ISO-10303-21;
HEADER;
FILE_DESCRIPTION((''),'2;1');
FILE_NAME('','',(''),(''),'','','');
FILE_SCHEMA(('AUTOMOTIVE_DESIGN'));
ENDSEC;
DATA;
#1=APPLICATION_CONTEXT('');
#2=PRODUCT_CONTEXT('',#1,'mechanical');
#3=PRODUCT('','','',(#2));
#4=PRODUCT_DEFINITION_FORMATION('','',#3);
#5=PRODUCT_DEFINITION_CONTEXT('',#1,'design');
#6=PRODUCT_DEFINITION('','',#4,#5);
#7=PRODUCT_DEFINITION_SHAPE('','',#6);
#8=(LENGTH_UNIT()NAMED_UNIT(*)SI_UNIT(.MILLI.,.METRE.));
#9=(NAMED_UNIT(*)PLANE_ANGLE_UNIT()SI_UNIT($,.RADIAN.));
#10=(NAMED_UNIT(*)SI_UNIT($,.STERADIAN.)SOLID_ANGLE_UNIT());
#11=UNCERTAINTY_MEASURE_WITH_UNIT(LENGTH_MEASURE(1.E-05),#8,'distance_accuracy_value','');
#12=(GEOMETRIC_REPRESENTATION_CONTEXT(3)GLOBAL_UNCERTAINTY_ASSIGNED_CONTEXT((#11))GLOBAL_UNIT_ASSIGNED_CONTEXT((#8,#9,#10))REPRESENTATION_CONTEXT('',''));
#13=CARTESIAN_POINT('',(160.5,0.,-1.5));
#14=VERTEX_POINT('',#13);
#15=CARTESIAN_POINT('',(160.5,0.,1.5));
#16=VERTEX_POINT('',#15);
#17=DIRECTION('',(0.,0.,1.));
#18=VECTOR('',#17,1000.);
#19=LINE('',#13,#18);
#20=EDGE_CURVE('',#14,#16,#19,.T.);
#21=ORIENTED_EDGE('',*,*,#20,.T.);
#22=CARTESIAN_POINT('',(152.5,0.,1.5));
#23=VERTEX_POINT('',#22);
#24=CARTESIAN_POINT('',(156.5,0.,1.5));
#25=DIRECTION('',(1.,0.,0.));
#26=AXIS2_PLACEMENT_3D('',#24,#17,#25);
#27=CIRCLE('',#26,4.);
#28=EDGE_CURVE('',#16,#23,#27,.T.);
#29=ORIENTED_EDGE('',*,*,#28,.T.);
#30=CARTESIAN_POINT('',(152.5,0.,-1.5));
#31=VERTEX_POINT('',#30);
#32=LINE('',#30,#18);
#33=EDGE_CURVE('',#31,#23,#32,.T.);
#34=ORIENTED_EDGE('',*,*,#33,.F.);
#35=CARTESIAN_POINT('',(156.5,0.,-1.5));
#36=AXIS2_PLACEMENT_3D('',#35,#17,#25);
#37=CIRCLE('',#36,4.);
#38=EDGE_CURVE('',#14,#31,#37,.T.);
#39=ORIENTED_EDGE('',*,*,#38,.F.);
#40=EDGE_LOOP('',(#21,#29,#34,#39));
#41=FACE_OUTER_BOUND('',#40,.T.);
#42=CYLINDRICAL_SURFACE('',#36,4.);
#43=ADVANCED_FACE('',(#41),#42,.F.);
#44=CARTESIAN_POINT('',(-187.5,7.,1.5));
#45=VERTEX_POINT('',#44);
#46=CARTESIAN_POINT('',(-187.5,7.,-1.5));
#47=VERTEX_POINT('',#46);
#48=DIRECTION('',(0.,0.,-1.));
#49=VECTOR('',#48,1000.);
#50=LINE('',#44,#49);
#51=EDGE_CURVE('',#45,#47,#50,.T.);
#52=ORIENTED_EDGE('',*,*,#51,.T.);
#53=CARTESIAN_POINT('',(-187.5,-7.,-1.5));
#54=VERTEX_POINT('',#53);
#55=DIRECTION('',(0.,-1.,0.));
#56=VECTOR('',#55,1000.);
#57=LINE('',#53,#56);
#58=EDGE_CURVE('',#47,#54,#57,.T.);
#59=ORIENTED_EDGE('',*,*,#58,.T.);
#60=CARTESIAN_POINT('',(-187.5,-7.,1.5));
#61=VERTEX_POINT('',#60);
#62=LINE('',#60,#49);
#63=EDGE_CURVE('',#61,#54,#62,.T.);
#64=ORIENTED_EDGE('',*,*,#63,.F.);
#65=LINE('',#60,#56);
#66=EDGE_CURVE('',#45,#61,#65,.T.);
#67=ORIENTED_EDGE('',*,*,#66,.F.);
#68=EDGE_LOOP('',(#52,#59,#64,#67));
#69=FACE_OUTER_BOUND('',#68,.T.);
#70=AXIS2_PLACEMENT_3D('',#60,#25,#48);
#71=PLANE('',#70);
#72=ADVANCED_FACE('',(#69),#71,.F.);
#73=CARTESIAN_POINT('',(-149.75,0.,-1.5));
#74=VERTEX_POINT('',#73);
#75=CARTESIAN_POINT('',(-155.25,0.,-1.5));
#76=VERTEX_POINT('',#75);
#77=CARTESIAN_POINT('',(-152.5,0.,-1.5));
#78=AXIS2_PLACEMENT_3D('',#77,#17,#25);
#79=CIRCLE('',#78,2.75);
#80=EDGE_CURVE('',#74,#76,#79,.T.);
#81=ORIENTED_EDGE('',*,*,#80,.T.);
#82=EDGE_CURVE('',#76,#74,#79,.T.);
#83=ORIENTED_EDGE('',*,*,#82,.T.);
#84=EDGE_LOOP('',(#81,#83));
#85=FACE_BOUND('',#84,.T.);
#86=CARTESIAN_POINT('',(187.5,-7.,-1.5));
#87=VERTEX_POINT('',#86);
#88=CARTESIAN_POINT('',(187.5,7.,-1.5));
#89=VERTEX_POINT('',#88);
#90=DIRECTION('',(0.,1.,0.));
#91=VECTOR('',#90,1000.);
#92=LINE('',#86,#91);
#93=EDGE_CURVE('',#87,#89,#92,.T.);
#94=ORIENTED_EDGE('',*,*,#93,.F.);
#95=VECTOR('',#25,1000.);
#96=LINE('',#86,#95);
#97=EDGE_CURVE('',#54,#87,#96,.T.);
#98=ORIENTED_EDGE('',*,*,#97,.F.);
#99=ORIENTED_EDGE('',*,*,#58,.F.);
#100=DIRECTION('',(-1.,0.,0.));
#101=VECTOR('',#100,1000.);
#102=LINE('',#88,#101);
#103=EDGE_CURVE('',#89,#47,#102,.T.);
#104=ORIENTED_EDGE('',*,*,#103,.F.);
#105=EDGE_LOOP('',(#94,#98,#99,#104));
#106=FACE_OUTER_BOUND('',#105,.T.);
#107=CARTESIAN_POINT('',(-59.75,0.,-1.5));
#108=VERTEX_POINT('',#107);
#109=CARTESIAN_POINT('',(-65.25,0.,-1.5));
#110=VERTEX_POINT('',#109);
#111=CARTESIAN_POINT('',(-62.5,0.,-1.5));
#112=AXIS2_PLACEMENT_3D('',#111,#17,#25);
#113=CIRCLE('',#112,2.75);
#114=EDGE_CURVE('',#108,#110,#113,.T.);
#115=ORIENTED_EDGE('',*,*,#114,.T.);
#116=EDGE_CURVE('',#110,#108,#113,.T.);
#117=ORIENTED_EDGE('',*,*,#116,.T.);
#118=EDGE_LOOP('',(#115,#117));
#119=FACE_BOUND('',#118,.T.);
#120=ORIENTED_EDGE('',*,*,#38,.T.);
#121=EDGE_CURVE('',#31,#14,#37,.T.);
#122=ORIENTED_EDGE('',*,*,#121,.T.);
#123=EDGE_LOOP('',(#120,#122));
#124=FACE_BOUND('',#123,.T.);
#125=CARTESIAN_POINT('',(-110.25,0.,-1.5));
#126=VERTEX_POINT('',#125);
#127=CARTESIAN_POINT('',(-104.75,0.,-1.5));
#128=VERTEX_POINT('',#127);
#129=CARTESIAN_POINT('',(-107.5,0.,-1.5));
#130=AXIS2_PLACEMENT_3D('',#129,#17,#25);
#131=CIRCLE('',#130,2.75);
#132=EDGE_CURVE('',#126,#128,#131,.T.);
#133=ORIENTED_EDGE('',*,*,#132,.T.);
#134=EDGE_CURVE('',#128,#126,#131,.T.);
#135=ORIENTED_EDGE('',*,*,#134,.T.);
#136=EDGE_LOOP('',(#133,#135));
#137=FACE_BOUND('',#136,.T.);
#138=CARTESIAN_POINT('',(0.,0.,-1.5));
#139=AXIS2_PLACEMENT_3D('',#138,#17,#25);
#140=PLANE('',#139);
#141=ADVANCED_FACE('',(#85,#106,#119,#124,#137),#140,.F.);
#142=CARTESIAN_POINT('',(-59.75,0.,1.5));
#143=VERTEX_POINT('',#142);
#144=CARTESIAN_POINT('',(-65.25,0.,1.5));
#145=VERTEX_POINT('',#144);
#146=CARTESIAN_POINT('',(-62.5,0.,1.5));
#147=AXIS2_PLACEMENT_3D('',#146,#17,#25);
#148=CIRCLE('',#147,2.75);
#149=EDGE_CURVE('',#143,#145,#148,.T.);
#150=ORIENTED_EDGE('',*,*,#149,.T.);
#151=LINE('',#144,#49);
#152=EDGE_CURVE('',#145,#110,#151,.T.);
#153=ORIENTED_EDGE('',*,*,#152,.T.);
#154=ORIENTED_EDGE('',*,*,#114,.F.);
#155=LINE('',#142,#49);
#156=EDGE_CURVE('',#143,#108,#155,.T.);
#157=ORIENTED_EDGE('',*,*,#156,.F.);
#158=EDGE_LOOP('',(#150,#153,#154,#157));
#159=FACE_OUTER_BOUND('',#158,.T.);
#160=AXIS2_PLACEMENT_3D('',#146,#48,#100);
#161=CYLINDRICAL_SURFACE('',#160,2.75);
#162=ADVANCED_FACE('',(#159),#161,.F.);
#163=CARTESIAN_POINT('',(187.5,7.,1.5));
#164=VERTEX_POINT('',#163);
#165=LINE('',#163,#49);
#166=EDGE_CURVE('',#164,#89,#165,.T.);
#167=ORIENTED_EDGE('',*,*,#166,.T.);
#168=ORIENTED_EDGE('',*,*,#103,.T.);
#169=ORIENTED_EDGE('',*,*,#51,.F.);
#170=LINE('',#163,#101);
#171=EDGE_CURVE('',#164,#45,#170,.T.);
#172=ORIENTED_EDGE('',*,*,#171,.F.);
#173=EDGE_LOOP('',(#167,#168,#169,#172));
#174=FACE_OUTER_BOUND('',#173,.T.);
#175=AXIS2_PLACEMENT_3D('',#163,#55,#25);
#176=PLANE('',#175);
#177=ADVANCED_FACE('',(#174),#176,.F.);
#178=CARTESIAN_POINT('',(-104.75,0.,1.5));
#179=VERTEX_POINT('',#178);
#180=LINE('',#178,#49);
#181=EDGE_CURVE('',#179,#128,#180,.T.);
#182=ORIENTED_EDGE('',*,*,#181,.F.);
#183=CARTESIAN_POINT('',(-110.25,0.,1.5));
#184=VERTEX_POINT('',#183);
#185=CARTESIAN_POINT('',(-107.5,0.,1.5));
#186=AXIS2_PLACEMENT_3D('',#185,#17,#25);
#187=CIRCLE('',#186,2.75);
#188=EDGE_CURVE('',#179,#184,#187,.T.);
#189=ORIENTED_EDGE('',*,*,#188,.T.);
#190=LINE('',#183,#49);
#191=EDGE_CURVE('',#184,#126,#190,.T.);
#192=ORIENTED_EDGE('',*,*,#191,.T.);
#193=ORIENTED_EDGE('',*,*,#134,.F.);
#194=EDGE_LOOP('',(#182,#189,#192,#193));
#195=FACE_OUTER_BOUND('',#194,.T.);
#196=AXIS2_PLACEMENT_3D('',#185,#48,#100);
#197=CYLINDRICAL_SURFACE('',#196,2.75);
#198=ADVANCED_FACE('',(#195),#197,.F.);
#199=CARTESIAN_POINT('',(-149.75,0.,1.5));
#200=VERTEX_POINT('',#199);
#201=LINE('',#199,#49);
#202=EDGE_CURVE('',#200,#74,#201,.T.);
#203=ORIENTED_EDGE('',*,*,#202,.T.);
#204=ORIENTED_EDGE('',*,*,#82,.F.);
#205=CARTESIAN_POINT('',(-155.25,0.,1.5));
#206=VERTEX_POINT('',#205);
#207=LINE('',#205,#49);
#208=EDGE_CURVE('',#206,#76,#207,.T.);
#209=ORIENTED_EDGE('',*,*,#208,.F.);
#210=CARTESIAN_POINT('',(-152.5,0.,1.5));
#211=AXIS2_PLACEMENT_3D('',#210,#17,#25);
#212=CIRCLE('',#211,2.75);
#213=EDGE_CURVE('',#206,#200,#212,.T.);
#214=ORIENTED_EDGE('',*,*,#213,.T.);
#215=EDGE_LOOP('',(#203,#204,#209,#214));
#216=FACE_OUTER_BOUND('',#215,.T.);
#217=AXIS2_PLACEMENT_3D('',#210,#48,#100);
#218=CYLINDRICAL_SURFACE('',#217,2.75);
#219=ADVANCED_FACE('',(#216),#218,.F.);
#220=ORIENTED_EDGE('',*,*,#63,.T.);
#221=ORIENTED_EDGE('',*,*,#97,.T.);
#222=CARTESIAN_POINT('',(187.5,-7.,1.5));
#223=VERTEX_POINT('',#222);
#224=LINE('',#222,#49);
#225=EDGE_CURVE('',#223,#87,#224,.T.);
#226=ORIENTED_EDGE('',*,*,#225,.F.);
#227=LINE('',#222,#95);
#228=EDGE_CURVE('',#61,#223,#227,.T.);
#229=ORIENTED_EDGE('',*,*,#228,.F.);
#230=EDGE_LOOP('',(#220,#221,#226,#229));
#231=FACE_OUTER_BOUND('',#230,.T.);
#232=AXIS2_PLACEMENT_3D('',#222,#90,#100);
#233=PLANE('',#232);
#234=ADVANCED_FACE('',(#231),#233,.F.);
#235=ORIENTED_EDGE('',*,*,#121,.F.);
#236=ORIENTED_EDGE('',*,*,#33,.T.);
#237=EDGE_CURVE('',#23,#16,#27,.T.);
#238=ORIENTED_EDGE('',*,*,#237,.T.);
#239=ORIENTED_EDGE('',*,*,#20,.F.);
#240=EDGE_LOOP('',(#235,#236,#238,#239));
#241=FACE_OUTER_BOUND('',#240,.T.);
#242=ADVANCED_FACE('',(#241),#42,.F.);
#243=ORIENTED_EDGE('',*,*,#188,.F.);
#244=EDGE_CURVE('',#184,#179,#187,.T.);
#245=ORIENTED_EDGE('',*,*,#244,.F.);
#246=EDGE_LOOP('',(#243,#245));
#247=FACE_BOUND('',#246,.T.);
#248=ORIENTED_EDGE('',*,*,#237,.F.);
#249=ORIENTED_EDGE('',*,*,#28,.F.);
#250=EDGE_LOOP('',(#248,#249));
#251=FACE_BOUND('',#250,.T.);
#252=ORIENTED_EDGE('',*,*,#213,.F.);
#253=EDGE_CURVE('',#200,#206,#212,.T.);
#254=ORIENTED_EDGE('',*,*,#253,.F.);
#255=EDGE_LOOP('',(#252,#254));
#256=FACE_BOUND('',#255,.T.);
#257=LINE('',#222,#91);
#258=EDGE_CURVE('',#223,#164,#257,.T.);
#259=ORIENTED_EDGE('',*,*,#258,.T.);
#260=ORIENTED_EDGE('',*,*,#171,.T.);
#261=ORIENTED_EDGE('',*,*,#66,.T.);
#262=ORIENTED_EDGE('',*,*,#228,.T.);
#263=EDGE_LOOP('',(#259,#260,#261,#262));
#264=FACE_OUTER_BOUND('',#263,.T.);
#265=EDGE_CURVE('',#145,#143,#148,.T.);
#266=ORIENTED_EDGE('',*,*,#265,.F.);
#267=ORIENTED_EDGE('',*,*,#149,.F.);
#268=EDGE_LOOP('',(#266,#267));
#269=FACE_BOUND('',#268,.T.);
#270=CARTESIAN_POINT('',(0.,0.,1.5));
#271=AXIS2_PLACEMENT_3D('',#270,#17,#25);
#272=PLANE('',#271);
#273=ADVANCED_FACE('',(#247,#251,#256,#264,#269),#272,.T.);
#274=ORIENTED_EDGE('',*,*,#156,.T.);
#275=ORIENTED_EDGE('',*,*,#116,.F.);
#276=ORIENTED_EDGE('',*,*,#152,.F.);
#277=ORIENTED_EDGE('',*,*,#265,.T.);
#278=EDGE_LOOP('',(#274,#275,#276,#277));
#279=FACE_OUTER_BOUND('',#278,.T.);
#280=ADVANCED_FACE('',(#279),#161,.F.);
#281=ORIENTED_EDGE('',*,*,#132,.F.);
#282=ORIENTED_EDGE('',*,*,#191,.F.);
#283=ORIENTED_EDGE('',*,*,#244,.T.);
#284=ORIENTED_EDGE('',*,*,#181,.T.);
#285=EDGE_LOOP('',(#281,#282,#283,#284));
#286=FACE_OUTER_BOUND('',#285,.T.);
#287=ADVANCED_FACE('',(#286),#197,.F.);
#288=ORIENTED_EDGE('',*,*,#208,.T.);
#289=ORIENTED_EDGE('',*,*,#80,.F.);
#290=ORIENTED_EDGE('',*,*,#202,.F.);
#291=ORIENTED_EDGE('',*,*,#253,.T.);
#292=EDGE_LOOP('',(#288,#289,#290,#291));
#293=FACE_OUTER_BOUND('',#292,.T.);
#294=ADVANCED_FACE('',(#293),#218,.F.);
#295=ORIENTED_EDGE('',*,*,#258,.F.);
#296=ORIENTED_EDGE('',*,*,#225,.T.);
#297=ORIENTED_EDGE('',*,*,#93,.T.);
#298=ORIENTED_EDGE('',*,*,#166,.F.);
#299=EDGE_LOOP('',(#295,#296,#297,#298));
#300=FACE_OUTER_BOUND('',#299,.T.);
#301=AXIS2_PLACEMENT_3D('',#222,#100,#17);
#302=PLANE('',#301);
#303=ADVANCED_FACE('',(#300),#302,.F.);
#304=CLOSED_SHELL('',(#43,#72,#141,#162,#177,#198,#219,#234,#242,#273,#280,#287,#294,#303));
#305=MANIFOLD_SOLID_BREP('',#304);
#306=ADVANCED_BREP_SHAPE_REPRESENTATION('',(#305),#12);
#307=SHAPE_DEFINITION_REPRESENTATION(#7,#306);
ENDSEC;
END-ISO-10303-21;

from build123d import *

# Parameters (mm, degrees)
SKETCH_1_W          = 375
SKETCH_1_H          = 14
SKETCH_1_R          = 2.75
EXTRUDE_1_DEPTH     = 1.5
SKETCH_2_R          = 4
CUT_EXTRUDE_1_DEPTH = 3


with BuildPart() as part:
    # 草图1 → 凸台-拉伸1 (new, symmetric)
    with BuildSketch(Plane.XY):
        Rectangle(SKETCH_1_W, SKETCH_1_H)
        with Locations((-152.5, 0)):
            Circle(SKETCH_1_R, mode=Mode.SUBTRACT)
        with Locations((-107.5, 0)):
            Circle(SKETCH_1_R, mode=Mode.SUBTRACT)
        with Locations((-62.5, 0)):
            Circle(SKETCH_1_R, mode=Mode.SUBTRACT)
    extrude(amount=EXTRUDE_1_DEPTH, both=True)

    # 草图2 → 切除-拉伸1 (cut)
    with BuildSketch(Plane.XY.offset(1.5)):
        with Locations((156.5, 0)):
            Circle(SKETCH_2_R)
    extrude(amount=-CUT_EXTRUDE_1_DEPTH, mode=Mode.SUBTRACT)


solid = part.part
